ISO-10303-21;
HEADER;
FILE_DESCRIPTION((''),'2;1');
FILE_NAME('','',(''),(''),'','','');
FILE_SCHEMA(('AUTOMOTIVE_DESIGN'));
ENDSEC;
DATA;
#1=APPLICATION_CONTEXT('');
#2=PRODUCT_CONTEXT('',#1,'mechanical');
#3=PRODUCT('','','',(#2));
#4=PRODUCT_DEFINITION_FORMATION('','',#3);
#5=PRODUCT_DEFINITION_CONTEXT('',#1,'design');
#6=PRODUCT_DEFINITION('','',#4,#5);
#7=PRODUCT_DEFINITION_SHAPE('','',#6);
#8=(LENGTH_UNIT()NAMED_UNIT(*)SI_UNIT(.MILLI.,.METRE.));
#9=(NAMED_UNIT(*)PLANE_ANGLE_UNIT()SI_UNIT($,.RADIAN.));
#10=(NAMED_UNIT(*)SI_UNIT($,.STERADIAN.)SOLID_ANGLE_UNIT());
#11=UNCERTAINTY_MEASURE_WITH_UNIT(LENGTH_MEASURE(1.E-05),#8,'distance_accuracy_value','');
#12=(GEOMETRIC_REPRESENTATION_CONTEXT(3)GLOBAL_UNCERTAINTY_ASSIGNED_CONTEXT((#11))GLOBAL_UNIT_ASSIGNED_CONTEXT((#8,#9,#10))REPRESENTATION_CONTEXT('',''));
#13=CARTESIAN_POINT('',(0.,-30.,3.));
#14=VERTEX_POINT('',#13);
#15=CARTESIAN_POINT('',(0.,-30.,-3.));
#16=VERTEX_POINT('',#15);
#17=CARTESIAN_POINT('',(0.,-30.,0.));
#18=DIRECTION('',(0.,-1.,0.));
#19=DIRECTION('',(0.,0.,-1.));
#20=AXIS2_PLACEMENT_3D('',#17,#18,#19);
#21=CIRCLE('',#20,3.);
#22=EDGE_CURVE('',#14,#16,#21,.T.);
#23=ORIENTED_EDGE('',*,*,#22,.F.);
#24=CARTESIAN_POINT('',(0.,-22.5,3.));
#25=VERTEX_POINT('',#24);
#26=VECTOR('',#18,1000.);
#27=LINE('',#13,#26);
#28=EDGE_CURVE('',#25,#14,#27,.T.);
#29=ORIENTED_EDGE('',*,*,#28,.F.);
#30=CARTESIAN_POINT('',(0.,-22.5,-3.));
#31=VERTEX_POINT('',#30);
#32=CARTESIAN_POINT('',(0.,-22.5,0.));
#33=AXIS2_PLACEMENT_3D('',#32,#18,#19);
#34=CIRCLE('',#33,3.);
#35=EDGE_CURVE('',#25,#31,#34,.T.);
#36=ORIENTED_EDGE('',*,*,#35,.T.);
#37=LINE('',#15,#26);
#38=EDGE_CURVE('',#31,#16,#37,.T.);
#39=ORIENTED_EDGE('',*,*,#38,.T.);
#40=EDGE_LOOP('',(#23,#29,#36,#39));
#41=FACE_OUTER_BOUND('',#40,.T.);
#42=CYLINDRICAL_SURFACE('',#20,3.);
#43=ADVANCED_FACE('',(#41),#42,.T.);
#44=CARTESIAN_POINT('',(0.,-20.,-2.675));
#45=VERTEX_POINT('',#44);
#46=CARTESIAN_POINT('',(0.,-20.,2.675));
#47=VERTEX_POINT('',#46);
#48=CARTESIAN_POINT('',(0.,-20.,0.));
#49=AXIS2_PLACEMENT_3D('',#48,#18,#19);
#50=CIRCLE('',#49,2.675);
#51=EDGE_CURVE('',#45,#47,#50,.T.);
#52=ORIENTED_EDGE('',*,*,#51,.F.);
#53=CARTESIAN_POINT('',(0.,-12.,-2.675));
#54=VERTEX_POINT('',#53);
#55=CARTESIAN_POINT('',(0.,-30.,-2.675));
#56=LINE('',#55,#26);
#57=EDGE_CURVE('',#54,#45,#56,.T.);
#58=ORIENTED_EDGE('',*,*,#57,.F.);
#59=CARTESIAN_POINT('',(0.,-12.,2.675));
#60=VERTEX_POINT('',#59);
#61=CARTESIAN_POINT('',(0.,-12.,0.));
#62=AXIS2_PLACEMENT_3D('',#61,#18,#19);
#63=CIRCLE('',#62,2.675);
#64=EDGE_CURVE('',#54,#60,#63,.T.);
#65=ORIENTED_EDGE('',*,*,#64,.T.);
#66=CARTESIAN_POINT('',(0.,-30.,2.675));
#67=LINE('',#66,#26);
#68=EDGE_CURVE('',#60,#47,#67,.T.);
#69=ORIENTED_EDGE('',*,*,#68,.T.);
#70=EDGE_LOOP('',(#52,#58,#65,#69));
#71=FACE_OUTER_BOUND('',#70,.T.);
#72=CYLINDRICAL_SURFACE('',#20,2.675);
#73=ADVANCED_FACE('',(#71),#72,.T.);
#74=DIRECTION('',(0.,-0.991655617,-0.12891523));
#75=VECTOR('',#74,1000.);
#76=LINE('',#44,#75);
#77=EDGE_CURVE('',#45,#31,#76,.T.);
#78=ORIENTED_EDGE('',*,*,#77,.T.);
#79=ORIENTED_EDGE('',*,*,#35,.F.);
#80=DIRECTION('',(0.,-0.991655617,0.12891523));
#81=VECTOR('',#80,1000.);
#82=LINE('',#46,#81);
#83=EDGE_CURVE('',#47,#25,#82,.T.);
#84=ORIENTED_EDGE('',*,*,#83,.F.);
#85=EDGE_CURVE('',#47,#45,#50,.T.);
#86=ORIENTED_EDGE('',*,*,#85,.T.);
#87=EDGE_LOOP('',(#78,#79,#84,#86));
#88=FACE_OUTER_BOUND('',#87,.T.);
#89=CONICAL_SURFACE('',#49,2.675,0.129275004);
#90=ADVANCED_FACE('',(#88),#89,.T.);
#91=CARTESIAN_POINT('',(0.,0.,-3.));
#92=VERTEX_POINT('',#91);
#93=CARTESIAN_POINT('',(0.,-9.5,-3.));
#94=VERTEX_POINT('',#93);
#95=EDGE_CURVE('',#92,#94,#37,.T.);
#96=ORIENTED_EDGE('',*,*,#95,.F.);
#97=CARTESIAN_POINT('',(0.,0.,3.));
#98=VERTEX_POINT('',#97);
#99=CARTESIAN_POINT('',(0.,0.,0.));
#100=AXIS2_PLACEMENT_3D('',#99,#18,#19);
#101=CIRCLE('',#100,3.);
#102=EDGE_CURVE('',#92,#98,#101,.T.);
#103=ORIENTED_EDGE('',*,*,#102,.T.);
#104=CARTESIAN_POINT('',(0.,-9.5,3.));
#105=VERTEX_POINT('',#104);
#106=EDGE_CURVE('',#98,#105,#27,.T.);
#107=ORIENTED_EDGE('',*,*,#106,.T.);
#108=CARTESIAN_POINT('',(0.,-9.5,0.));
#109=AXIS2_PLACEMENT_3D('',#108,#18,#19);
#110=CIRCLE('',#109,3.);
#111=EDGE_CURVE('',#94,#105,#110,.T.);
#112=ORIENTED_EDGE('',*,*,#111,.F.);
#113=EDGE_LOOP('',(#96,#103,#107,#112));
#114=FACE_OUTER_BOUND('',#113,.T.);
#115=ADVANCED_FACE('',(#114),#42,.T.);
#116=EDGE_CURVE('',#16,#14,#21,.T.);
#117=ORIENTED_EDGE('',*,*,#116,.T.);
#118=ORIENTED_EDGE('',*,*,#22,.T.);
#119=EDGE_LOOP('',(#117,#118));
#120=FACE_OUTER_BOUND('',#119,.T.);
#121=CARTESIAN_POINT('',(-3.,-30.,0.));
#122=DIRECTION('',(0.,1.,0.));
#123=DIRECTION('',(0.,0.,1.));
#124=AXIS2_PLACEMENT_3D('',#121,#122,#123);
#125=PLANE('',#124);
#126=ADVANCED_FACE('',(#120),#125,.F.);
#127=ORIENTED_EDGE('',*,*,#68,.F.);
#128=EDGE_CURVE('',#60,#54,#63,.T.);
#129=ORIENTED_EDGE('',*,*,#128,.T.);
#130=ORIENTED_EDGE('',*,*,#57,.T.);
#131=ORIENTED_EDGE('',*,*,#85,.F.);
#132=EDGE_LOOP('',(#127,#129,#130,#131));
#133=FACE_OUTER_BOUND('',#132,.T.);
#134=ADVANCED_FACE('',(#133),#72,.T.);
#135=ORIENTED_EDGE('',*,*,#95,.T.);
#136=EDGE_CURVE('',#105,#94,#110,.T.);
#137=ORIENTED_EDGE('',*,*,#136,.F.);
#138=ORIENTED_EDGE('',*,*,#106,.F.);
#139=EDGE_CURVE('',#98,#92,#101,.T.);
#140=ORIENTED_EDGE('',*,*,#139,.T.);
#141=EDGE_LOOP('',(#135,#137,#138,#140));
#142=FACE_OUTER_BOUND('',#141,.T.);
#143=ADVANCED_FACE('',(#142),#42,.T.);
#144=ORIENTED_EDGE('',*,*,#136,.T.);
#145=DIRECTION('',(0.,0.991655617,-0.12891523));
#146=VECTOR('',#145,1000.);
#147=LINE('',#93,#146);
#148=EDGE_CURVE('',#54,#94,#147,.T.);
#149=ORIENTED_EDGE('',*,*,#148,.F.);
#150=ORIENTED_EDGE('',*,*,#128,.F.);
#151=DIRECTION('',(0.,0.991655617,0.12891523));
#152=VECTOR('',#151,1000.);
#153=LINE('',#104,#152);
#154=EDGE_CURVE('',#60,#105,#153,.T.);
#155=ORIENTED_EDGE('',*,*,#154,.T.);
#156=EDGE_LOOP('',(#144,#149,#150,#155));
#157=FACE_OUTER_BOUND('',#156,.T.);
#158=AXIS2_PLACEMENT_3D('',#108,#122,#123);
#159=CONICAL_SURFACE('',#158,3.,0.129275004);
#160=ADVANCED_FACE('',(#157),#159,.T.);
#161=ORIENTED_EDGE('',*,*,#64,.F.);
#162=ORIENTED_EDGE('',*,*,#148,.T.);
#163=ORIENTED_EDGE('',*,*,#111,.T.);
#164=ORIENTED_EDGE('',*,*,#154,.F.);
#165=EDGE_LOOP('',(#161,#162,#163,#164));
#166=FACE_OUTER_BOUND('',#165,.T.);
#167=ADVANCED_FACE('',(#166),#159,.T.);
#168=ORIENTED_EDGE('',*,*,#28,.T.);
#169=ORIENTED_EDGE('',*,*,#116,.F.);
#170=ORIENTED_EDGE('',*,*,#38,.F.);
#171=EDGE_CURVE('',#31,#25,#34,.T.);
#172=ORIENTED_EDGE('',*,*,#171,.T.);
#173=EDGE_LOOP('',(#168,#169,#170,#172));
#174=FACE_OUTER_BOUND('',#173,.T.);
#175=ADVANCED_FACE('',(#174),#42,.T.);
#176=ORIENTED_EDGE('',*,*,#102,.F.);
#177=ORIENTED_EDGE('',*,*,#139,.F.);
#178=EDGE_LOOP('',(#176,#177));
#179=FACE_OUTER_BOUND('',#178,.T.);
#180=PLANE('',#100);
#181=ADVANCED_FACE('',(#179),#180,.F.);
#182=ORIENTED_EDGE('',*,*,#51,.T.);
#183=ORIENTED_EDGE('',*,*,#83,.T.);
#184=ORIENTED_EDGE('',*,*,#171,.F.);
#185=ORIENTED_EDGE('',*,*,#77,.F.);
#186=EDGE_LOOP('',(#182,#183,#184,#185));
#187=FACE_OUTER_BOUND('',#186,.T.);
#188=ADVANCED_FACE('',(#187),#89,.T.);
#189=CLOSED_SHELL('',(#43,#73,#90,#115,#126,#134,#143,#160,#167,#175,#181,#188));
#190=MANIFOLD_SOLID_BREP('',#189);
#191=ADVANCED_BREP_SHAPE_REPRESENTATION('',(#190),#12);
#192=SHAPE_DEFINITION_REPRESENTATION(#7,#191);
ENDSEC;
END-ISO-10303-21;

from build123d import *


with BuildPart() as part:
    # Sketch1 → Revolve1 (revolve)
    with BuildSketch(Plane.XY, mode=Mode.PRIVATE) as revolve1_sk:
        Polygon((0, 0), (-3, 0), (-3, -9.5), (-2.675, -12), (-2.675, -20), (-3, -22.5), (-3, -30), (0, -30), align=None)
    revolve(revolve1_sk.sketch.rotate(Axis((0, -30, 0), (0, 1, 0)), 270), axis=Axis((0, -30, 0), (0, 1, 0)))


solid = part.part
